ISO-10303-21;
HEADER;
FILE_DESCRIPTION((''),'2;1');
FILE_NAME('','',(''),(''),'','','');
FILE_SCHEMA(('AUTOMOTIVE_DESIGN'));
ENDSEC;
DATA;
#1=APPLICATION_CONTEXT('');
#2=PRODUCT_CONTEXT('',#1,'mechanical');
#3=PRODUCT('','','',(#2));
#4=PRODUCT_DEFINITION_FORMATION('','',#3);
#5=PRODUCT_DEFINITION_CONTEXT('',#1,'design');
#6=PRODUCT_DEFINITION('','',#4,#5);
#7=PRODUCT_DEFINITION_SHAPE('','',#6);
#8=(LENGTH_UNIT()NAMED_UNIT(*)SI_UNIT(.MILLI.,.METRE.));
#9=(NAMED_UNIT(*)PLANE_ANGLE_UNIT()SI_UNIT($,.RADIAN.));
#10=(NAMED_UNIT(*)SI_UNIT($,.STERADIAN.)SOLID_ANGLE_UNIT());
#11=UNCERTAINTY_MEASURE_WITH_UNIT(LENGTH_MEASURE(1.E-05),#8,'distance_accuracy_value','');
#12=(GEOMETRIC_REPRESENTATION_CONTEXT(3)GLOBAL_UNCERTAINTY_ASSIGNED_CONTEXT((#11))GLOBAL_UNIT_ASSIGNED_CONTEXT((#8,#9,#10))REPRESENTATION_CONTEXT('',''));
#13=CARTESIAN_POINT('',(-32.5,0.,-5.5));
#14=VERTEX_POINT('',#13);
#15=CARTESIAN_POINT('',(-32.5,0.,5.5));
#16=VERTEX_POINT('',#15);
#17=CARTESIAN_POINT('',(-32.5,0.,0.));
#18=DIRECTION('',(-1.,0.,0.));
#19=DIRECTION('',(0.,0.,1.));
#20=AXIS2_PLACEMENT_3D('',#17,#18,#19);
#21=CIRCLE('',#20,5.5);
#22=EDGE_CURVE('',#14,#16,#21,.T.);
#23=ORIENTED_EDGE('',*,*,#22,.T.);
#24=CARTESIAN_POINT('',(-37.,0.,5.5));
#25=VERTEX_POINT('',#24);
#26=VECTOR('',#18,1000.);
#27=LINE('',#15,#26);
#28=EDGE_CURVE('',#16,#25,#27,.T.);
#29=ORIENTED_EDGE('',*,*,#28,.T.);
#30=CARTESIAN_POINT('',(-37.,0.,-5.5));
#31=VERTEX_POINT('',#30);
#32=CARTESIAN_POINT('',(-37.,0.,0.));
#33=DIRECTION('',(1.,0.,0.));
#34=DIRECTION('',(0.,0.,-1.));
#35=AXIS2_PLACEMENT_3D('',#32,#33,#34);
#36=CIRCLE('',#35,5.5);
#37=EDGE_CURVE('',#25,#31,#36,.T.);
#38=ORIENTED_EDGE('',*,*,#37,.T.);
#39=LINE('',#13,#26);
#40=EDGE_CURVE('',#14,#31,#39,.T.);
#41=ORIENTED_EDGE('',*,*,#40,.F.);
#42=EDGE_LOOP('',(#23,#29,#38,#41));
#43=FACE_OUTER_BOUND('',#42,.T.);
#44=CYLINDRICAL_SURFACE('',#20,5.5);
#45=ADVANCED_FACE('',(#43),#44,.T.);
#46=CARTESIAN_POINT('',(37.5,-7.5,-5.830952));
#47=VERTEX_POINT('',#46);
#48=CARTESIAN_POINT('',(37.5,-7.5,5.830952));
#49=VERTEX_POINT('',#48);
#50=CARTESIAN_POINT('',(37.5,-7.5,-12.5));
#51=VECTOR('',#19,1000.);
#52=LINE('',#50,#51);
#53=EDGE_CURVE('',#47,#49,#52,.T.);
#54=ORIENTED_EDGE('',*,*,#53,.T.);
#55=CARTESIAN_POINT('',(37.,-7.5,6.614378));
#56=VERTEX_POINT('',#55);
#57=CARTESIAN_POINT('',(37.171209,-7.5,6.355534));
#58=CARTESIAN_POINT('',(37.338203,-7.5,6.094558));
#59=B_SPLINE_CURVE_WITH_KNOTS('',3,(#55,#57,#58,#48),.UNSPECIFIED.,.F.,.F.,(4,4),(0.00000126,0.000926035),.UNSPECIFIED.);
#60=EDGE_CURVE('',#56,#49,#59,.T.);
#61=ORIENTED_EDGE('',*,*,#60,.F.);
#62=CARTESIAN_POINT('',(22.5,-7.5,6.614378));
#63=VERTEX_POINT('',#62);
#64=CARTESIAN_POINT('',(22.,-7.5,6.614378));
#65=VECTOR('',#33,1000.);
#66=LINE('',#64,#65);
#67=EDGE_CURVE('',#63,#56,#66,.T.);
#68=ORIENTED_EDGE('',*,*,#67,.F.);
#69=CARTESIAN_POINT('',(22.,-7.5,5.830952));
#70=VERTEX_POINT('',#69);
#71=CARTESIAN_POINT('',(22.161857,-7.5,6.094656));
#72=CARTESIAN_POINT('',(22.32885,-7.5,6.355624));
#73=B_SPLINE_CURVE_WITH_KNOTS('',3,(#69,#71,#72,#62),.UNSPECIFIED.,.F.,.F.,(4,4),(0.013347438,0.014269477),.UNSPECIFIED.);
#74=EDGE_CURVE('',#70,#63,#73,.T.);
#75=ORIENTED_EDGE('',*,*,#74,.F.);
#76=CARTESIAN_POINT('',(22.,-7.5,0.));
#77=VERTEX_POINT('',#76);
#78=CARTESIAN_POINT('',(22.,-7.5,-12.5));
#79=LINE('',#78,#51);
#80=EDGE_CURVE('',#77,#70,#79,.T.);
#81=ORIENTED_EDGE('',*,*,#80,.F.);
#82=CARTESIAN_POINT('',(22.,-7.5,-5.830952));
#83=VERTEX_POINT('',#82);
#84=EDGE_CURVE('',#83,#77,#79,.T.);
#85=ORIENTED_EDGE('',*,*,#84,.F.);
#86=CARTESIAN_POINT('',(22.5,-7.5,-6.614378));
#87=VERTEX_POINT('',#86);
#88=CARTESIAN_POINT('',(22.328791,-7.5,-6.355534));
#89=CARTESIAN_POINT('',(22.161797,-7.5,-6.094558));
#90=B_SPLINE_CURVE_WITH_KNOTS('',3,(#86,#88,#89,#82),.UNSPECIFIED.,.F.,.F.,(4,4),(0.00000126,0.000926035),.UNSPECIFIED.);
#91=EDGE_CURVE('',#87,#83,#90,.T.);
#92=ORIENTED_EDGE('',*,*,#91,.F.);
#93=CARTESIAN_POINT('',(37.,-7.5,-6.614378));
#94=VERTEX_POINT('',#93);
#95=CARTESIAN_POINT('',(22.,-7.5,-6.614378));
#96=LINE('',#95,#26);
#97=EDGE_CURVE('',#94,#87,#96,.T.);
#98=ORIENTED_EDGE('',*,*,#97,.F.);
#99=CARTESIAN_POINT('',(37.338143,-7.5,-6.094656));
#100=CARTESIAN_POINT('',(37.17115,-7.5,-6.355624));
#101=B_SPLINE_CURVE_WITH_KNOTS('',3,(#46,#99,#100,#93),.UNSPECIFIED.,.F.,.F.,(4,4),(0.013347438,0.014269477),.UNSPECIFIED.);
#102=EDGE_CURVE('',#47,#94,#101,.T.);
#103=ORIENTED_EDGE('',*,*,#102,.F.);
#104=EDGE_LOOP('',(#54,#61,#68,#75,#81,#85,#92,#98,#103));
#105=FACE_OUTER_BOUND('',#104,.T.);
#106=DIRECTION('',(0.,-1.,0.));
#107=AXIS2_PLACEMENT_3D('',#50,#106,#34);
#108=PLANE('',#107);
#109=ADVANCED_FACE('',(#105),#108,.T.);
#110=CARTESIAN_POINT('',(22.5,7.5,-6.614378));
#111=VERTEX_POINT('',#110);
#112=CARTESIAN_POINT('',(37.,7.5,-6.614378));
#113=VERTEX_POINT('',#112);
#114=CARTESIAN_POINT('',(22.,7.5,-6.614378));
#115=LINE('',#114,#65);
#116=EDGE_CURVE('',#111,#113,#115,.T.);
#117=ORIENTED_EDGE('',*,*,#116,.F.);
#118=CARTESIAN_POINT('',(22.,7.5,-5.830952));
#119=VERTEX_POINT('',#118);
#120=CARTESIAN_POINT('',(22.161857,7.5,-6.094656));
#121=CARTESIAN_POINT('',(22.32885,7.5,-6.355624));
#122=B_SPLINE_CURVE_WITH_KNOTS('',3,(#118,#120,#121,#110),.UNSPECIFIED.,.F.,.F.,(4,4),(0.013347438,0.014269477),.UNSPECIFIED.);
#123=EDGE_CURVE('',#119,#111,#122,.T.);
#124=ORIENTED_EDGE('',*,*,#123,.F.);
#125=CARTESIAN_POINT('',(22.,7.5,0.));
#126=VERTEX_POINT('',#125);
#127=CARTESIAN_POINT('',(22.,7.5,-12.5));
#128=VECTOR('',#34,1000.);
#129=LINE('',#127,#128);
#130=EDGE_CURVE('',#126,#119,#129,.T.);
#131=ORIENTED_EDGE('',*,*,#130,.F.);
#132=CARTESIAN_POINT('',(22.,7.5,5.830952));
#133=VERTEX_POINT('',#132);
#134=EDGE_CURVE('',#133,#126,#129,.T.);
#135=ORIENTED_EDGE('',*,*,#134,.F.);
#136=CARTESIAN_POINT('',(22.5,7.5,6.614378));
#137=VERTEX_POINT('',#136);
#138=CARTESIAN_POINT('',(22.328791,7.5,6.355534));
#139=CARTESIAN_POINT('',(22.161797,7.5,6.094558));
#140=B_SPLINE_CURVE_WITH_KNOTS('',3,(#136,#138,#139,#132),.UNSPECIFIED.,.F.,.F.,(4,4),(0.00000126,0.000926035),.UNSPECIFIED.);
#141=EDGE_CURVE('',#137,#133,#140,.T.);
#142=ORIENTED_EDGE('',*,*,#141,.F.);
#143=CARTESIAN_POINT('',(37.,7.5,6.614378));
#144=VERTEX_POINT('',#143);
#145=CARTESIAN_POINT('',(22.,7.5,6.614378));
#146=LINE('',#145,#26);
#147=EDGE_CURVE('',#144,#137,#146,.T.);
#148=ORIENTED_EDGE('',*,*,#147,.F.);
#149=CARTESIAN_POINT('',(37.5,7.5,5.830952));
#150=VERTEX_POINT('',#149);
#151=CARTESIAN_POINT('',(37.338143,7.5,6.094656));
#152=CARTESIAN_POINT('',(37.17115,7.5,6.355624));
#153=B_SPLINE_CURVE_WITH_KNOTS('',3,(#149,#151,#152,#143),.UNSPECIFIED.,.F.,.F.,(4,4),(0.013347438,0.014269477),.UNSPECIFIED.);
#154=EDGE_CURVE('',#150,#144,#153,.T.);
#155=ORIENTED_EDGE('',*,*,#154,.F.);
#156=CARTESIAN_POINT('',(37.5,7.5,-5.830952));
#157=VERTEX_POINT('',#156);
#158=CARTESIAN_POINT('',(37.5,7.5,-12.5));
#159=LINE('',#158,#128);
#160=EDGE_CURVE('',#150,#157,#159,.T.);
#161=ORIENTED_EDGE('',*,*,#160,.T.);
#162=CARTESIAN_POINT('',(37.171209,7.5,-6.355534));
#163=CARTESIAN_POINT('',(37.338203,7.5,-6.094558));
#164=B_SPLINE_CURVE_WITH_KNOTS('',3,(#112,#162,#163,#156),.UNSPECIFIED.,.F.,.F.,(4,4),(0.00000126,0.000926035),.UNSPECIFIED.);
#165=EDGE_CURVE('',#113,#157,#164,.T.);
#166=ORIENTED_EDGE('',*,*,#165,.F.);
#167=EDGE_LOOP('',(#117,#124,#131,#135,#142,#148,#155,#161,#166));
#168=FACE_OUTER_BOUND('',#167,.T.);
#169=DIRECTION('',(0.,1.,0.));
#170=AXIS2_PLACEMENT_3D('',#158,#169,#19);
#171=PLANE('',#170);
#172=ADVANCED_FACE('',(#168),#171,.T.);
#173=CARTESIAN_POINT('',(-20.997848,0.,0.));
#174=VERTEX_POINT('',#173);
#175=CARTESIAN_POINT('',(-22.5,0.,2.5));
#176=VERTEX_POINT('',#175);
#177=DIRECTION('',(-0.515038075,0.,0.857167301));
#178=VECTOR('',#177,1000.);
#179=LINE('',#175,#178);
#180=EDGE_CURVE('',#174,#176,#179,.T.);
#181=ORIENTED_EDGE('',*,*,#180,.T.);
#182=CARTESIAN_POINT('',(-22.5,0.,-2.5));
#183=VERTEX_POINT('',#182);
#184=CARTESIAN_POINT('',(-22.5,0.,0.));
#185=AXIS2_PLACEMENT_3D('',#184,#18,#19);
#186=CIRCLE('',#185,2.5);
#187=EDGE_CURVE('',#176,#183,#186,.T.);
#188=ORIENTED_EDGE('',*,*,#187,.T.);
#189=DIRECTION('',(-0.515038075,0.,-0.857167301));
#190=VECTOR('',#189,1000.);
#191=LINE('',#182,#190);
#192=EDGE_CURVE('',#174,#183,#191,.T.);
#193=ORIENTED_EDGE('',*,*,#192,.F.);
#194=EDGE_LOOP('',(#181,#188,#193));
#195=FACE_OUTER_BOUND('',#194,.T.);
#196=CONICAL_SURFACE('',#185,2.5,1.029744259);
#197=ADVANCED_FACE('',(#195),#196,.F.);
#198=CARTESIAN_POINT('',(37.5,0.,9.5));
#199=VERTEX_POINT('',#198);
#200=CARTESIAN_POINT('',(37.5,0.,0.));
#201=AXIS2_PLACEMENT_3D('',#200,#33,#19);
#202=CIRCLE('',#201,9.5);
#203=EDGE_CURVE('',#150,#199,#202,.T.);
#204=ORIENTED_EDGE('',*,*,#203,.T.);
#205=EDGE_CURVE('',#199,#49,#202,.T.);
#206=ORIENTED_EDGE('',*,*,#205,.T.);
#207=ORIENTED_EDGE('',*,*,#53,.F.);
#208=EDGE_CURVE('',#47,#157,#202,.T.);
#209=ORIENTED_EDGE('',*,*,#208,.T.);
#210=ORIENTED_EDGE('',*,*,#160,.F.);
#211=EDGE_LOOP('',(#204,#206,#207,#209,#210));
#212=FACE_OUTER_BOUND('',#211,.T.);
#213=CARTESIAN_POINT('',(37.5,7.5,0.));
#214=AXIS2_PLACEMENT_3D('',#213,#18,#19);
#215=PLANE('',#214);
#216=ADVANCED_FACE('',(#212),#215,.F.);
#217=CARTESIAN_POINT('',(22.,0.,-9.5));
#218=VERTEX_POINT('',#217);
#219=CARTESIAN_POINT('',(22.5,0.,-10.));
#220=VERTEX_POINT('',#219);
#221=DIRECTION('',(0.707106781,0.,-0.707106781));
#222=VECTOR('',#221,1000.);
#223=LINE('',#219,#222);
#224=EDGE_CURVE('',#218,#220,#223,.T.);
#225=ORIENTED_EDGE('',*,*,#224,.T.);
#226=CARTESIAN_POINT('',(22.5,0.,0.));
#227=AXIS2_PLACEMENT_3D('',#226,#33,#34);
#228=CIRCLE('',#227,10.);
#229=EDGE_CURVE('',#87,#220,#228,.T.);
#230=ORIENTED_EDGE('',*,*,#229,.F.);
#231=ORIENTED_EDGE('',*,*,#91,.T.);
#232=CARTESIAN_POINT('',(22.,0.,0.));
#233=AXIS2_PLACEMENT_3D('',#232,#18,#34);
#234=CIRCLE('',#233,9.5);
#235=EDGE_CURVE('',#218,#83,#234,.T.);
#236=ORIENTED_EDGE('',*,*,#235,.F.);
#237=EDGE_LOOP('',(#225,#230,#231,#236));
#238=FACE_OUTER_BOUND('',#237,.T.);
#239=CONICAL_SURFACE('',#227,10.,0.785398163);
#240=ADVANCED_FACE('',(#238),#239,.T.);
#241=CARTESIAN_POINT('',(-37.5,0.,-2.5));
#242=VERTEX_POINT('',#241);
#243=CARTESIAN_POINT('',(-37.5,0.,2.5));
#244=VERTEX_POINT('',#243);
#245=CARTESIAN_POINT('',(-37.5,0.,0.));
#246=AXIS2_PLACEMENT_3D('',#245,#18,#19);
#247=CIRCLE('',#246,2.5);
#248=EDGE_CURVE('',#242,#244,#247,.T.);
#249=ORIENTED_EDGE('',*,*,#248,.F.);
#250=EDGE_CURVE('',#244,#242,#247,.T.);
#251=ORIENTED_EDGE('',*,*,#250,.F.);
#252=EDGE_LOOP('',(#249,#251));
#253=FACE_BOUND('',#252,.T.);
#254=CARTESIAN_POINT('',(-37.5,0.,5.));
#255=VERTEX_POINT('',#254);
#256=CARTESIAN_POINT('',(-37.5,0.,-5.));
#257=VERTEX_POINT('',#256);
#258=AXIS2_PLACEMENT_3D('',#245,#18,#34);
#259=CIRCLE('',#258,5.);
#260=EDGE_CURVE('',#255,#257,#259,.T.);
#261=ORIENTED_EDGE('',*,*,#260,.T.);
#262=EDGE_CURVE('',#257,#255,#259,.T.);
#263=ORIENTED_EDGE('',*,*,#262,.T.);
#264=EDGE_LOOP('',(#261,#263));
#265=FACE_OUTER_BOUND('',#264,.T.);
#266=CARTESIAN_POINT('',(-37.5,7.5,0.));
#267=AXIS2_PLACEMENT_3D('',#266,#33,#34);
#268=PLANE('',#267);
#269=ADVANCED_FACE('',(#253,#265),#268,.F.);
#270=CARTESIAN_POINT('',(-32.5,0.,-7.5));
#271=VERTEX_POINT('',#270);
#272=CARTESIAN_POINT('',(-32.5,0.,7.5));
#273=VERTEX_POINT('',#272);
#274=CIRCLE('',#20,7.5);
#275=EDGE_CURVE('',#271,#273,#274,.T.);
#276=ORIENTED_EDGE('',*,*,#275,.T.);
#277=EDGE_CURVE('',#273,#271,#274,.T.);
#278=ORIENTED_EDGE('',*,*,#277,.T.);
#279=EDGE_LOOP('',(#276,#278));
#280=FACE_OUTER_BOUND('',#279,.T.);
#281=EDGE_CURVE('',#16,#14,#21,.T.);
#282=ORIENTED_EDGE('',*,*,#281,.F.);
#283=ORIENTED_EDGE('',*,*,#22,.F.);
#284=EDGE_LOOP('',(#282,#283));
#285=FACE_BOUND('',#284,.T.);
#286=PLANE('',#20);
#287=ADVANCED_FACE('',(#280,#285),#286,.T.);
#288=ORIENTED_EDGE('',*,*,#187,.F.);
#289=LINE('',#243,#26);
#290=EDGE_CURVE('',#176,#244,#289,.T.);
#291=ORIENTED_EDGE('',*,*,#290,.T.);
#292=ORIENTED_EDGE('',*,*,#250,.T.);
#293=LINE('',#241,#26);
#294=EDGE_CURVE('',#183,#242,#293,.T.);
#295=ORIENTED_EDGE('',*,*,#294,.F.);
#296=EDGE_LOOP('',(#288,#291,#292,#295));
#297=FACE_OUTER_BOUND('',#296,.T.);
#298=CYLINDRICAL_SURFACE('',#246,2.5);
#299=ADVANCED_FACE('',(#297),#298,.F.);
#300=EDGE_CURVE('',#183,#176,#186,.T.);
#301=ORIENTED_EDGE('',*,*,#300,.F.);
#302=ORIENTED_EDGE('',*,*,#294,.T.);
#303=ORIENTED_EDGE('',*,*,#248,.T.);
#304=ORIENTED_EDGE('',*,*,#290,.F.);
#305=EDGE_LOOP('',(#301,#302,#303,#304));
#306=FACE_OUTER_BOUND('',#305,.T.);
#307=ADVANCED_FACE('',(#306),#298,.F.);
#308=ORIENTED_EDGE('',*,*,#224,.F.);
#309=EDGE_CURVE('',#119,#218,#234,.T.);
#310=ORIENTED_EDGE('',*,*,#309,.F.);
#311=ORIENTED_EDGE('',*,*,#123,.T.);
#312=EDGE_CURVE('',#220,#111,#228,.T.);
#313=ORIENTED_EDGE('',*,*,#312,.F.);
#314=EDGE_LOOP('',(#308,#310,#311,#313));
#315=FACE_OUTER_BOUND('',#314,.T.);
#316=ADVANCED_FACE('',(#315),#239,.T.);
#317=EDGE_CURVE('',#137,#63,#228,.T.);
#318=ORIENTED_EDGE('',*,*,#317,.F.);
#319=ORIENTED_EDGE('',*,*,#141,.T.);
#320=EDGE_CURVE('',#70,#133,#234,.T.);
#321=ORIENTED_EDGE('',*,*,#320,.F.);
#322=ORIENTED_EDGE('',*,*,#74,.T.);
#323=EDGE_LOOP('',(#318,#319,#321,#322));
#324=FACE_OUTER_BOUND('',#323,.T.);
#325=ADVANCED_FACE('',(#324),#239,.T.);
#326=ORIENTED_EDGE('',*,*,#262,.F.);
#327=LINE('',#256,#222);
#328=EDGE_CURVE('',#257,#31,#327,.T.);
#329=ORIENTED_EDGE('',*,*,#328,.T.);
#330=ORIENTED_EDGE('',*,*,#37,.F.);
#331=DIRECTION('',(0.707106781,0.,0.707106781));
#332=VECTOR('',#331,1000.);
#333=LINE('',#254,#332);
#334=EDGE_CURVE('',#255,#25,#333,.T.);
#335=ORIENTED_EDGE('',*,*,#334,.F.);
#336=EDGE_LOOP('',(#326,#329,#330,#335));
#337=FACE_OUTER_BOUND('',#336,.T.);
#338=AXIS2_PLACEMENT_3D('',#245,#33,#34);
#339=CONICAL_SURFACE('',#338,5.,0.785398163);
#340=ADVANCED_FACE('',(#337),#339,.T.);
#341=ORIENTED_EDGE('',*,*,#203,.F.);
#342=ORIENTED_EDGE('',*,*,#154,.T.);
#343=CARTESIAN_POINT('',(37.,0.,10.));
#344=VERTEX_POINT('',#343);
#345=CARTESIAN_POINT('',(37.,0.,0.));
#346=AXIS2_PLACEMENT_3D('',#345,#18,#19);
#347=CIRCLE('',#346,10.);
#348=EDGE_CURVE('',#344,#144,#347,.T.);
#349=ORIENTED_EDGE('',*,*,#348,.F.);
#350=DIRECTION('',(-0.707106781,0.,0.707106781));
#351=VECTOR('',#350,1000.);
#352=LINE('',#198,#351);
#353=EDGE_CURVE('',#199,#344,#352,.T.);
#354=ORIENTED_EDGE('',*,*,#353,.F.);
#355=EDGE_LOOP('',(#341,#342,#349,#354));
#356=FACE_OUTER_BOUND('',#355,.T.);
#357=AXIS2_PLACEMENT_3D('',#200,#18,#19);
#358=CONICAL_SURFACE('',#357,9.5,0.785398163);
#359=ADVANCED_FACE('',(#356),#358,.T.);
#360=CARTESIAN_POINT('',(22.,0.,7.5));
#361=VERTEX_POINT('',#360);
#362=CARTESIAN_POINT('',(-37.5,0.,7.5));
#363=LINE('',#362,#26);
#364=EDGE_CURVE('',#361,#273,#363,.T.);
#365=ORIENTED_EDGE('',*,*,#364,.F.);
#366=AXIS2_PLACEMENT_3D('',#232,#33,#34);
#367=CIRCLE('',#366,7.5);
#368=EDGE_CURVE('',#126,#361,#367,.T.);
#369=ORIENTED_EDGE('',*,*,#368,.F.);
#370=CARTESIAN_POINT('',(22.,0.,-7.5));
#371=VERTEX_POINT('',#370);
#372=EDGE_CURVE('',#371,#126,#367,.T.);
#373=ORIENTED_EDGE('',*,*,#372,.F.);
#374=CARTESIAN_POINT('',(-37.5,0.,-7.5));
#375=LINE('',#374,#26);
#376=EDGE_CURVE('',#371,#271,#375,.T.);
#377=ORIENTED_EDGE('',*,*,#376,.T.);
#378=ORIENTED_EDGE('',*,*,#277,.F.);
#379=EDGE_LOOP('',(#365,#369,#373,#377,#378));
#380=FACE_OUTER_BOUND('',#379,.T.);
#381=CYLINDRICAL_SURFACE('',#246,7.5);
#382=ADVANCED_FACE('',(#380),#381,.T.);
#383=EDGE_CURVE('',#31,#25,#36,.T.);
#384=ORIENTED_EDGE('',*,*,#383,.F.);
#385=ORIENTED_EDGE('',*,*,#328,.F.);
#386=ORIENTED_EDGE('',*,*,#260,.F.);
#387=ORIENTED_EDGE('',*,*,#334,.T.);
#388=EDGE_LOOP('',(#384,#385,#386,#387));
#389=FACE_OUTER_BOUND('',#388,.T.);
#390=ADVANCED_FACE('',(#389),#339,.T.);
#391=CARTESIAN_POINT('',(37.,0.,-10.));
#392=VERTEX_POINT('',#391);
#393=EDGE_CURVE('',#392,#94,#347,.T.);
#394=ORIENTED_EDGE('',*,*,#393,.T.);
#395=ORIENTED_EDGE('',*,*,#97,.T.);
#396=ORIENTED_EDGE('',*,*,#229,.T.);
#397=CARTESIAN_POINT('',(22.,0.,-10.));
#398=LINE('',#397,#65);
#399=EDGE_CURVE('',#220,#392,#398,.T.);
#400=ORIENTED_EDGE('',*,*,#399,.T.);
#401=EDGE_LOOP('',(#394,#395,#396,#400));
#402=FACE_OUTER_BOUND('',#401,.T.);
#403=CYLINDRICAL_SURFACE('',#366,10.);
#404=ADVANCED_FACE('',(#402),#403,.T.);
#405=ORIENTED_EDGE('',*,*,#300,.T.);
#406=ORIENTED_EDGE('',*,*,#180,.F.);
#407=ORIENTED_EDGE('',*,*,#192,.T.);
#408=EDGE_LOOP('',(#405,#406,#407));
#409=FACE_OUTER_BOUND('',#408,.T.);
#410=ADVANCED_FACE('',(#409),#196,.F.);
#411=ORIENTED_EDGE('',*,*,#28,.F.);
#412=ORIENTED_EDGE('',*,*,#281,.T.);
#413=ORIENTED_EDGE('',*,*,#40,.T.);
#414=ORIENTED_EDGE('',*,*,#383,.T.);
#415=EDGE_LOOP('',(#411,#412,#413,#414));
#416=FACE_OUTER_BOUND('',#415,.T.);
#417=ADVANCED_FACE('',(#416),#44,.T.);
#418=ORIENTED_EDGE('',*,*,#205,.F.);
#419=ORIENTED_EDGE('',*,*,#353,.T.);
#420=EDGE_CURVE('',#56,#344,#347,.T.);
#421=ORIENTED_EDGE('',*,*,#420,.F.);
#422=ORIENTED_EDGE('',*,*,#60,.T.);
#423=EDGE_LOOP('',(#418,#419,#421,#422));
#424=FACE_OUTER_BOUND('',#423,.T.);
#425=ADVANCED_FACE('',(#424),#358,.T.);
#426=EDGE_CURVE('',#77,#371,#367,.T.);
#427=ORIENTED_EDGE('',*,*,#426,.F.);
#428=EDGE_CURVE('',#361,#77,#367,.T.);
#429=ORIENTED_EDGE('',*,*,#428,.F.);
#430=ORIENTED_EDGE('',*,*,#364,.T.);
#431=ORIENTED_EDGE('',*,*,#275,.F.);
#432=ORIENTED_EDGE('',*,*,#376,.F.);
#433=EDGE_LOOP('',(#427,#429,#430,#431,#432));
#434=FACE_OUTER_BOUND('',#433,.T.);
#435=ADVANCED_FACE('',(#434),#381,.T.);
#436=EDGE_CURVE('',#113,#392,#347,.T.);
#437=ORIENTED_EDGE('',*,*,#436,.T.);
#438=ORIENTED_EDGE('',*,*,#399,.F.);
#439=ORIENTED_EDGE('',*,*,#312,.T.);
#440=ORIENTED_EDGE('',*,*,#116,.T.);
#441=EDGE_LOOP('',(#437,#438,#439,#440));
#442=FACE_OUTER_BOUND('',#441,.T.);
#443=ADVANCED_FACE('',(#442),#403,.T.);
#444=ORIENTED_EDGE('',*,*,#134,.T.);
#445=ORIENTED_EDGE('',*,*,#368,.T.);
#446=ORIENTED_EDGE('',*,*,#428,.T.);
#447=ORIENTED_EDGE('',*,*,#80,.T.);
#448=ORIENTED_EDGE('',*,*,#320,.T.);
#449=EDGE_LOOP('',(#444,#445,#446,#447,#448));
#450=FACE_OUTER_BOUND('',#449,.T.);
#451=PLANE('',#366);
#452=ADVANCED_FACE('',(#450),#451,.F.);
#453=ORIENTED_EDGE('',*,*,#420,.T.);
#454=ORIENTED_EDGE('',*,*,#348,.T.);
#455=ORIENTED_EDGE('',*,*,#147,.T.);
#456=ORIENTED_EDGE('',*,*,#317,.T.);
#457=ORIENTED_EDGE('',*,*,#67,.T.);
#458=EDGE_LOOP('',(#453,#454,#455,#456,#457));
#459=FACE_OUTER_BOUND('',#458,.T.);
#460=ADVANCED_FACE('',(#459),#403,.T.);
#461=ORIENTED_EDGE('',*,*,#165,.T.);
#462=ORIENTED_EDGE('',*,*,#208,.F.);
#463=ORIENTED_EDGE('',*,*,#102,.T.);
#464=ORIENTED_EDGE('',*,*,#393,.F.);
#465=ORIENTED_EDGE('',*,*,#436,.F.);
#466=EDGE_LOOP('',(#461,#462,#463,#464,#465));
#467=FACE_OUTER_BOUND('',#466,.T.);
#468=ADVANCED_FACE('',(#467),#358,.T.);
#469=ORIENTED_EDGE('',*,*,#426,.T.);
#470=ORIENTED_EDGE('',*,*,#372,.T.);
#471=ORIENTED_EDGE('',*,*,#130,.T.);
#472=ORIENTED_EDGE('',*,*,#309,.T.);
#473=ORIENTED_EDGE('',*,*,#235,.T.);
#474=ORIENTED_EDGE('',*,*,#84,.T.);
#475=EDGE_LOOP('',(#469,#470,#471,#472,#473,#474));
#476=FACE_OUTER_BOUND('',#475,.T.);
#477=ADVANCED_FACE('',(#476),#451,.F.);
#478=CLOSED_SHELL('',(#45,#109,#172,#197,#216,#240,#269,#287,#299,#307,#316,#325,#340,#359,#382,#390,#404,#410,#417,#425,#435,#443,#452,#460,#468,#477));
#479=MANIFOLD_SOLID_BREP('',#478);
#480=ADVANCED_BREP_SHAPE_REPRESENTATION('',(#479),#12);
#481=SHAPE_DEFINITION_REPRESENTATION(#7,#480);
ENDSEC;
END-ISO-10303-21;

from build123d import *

# Parameters (mm, degrees)
SKETCH1_W             = 75
SKETCH1_H             = 7.5
CHAMFER3_SIZE         = 0.5
M6_TAPPED_HOLE1_D     = 5
M6_TAPPED_HOLE1_DEPTH = 15
M6_TAPPED_HOLE1_TIP   = 1.502151548
SKETCH7_R             = 10
BOSS_EXTRUDE2_DEPTH   = 15.5
CHAMFER4_SIZE         = 0.5
SKETCH8_OUTSIDE_W     = 38.032
SKETCH8_OUTSIDE_H     = 38.032
SKETCH8_OUTSIDE_W_2   = 25
SKETCH8_OUTSIDE_H_2   = 15
CUT_EXTRUDE1_DEPTH    = 62.15758334
SKETCH11_OUTSIDE_W    = 37.812
SKETCH11_OUTSIDE_H    = 32.812
SKETCH11_OUTSIDE_R    = 5.5
CUT_EXTRUDE2_DEPTH    = 5
CHAMFER5_SIZE         = 0.5


with BuildPart() as part:
    # Sketch1 → Revolve1 (revolve)
    with BuildSketch(Plane.XY, mode=Mode.PRIVATE) as revolve1_sk:
        with Locations((0, 3.75)):
            Rectangle(SKETCH1_W, SKETCH1_H)
    revolve(revolve1_sk.sketch.rotate(Axis((-37.5, 0, 0), (1, 0, 0)), 90), axis=Axis((-37.5, 0, 0), (1, 0, 0)))

    # Chamfer3
    chamfer3_edges = [part.edges().sort_by_distance(p)[0] for p in [
        (-37.5, 0, -7.5),
    ]]
    chamfer(chamfer3_edges, length=CHAMFER3_SIZE)

    # M6 Tapped Hole1
    with Locations(Plane.ZY.offset(37.5)):
        with Locations((0, 0)):
            Hole(M6_TAPPED_HOLE1_D / 2, depth=M6_TAPPED_HOLE1_DEPTH)
            with Locations((0, 0, -(M6_TAPPED_HOLE1_DEPTH + M6_TAPPED_HOLE1_TIP / 2))):  # 118° drill point
                Cone(0, M6_TAPPED_HOLE1_D / 2, M6_TAPPED_HOLE1_TIP, mode=Mode.SUBTRACT)

    # Sketch7 → Boss-Extrude2 (add)
    with BuildSketch(Plane(origin=(37.5, 0, 0), x_dir=(0, 0, -1), z_dir=(1, 0, 0))):
        Circle(SKETCH7_R)
    extrude(amount=-BOSS_EXTRUDE2_DEPTH)

    # Chamfer4
    chamfer4_edges = [part.edges().sort_by_distance(p)[0] for p in [
        (22, 0, 10),
        (37.5, 0, 10),
    ]]
    chamfer(chamfer4_edges, length=CHAMFER4_SIZE)

    # Sketch8 outside → Cut-Extrude1 (cut, through all)
    with BuildSketch(Plane.ZY.offset(-22)):
        Rectangle(SKETCH8_OUTSIDE_W, SKETCH8_OUTSIDE_H)
        Rectangle(SKETCH8_OUTSIDE_W_2, SKETCH8_OUTSIDE_H_2, mode=Mode.SUBTRACT)
    extrude(amount=-CUT_EXTRUDE1_DEPTH, mode=Mode.SUBTRACT)

    # Sketch11 outside → Cut-Extrude2 (cut)
    with BuildSketch(Plane.ZY.offset(37.5)):
        Rectangle(SKETCH11_OUTSIDE_W, SKETCH11_OUTSIDE_H)
        Circle(SKETCH11_OUTSIDE_R, mode=Mode.SUBTRACT)
    extrude(amount=-CUT_EXTRUDE2_DEPTH, mode=Mode.SUBTRACT)

    # Chamfer5
    chamfer5_edges = [part.edges().sort_by_distance(p)[0] for p in [
        (-37.5, 0, -5.5),
    ]]
    chamfer(chamfer5_edges, length=CHAMFER5_SIZE)


solid = part.part
